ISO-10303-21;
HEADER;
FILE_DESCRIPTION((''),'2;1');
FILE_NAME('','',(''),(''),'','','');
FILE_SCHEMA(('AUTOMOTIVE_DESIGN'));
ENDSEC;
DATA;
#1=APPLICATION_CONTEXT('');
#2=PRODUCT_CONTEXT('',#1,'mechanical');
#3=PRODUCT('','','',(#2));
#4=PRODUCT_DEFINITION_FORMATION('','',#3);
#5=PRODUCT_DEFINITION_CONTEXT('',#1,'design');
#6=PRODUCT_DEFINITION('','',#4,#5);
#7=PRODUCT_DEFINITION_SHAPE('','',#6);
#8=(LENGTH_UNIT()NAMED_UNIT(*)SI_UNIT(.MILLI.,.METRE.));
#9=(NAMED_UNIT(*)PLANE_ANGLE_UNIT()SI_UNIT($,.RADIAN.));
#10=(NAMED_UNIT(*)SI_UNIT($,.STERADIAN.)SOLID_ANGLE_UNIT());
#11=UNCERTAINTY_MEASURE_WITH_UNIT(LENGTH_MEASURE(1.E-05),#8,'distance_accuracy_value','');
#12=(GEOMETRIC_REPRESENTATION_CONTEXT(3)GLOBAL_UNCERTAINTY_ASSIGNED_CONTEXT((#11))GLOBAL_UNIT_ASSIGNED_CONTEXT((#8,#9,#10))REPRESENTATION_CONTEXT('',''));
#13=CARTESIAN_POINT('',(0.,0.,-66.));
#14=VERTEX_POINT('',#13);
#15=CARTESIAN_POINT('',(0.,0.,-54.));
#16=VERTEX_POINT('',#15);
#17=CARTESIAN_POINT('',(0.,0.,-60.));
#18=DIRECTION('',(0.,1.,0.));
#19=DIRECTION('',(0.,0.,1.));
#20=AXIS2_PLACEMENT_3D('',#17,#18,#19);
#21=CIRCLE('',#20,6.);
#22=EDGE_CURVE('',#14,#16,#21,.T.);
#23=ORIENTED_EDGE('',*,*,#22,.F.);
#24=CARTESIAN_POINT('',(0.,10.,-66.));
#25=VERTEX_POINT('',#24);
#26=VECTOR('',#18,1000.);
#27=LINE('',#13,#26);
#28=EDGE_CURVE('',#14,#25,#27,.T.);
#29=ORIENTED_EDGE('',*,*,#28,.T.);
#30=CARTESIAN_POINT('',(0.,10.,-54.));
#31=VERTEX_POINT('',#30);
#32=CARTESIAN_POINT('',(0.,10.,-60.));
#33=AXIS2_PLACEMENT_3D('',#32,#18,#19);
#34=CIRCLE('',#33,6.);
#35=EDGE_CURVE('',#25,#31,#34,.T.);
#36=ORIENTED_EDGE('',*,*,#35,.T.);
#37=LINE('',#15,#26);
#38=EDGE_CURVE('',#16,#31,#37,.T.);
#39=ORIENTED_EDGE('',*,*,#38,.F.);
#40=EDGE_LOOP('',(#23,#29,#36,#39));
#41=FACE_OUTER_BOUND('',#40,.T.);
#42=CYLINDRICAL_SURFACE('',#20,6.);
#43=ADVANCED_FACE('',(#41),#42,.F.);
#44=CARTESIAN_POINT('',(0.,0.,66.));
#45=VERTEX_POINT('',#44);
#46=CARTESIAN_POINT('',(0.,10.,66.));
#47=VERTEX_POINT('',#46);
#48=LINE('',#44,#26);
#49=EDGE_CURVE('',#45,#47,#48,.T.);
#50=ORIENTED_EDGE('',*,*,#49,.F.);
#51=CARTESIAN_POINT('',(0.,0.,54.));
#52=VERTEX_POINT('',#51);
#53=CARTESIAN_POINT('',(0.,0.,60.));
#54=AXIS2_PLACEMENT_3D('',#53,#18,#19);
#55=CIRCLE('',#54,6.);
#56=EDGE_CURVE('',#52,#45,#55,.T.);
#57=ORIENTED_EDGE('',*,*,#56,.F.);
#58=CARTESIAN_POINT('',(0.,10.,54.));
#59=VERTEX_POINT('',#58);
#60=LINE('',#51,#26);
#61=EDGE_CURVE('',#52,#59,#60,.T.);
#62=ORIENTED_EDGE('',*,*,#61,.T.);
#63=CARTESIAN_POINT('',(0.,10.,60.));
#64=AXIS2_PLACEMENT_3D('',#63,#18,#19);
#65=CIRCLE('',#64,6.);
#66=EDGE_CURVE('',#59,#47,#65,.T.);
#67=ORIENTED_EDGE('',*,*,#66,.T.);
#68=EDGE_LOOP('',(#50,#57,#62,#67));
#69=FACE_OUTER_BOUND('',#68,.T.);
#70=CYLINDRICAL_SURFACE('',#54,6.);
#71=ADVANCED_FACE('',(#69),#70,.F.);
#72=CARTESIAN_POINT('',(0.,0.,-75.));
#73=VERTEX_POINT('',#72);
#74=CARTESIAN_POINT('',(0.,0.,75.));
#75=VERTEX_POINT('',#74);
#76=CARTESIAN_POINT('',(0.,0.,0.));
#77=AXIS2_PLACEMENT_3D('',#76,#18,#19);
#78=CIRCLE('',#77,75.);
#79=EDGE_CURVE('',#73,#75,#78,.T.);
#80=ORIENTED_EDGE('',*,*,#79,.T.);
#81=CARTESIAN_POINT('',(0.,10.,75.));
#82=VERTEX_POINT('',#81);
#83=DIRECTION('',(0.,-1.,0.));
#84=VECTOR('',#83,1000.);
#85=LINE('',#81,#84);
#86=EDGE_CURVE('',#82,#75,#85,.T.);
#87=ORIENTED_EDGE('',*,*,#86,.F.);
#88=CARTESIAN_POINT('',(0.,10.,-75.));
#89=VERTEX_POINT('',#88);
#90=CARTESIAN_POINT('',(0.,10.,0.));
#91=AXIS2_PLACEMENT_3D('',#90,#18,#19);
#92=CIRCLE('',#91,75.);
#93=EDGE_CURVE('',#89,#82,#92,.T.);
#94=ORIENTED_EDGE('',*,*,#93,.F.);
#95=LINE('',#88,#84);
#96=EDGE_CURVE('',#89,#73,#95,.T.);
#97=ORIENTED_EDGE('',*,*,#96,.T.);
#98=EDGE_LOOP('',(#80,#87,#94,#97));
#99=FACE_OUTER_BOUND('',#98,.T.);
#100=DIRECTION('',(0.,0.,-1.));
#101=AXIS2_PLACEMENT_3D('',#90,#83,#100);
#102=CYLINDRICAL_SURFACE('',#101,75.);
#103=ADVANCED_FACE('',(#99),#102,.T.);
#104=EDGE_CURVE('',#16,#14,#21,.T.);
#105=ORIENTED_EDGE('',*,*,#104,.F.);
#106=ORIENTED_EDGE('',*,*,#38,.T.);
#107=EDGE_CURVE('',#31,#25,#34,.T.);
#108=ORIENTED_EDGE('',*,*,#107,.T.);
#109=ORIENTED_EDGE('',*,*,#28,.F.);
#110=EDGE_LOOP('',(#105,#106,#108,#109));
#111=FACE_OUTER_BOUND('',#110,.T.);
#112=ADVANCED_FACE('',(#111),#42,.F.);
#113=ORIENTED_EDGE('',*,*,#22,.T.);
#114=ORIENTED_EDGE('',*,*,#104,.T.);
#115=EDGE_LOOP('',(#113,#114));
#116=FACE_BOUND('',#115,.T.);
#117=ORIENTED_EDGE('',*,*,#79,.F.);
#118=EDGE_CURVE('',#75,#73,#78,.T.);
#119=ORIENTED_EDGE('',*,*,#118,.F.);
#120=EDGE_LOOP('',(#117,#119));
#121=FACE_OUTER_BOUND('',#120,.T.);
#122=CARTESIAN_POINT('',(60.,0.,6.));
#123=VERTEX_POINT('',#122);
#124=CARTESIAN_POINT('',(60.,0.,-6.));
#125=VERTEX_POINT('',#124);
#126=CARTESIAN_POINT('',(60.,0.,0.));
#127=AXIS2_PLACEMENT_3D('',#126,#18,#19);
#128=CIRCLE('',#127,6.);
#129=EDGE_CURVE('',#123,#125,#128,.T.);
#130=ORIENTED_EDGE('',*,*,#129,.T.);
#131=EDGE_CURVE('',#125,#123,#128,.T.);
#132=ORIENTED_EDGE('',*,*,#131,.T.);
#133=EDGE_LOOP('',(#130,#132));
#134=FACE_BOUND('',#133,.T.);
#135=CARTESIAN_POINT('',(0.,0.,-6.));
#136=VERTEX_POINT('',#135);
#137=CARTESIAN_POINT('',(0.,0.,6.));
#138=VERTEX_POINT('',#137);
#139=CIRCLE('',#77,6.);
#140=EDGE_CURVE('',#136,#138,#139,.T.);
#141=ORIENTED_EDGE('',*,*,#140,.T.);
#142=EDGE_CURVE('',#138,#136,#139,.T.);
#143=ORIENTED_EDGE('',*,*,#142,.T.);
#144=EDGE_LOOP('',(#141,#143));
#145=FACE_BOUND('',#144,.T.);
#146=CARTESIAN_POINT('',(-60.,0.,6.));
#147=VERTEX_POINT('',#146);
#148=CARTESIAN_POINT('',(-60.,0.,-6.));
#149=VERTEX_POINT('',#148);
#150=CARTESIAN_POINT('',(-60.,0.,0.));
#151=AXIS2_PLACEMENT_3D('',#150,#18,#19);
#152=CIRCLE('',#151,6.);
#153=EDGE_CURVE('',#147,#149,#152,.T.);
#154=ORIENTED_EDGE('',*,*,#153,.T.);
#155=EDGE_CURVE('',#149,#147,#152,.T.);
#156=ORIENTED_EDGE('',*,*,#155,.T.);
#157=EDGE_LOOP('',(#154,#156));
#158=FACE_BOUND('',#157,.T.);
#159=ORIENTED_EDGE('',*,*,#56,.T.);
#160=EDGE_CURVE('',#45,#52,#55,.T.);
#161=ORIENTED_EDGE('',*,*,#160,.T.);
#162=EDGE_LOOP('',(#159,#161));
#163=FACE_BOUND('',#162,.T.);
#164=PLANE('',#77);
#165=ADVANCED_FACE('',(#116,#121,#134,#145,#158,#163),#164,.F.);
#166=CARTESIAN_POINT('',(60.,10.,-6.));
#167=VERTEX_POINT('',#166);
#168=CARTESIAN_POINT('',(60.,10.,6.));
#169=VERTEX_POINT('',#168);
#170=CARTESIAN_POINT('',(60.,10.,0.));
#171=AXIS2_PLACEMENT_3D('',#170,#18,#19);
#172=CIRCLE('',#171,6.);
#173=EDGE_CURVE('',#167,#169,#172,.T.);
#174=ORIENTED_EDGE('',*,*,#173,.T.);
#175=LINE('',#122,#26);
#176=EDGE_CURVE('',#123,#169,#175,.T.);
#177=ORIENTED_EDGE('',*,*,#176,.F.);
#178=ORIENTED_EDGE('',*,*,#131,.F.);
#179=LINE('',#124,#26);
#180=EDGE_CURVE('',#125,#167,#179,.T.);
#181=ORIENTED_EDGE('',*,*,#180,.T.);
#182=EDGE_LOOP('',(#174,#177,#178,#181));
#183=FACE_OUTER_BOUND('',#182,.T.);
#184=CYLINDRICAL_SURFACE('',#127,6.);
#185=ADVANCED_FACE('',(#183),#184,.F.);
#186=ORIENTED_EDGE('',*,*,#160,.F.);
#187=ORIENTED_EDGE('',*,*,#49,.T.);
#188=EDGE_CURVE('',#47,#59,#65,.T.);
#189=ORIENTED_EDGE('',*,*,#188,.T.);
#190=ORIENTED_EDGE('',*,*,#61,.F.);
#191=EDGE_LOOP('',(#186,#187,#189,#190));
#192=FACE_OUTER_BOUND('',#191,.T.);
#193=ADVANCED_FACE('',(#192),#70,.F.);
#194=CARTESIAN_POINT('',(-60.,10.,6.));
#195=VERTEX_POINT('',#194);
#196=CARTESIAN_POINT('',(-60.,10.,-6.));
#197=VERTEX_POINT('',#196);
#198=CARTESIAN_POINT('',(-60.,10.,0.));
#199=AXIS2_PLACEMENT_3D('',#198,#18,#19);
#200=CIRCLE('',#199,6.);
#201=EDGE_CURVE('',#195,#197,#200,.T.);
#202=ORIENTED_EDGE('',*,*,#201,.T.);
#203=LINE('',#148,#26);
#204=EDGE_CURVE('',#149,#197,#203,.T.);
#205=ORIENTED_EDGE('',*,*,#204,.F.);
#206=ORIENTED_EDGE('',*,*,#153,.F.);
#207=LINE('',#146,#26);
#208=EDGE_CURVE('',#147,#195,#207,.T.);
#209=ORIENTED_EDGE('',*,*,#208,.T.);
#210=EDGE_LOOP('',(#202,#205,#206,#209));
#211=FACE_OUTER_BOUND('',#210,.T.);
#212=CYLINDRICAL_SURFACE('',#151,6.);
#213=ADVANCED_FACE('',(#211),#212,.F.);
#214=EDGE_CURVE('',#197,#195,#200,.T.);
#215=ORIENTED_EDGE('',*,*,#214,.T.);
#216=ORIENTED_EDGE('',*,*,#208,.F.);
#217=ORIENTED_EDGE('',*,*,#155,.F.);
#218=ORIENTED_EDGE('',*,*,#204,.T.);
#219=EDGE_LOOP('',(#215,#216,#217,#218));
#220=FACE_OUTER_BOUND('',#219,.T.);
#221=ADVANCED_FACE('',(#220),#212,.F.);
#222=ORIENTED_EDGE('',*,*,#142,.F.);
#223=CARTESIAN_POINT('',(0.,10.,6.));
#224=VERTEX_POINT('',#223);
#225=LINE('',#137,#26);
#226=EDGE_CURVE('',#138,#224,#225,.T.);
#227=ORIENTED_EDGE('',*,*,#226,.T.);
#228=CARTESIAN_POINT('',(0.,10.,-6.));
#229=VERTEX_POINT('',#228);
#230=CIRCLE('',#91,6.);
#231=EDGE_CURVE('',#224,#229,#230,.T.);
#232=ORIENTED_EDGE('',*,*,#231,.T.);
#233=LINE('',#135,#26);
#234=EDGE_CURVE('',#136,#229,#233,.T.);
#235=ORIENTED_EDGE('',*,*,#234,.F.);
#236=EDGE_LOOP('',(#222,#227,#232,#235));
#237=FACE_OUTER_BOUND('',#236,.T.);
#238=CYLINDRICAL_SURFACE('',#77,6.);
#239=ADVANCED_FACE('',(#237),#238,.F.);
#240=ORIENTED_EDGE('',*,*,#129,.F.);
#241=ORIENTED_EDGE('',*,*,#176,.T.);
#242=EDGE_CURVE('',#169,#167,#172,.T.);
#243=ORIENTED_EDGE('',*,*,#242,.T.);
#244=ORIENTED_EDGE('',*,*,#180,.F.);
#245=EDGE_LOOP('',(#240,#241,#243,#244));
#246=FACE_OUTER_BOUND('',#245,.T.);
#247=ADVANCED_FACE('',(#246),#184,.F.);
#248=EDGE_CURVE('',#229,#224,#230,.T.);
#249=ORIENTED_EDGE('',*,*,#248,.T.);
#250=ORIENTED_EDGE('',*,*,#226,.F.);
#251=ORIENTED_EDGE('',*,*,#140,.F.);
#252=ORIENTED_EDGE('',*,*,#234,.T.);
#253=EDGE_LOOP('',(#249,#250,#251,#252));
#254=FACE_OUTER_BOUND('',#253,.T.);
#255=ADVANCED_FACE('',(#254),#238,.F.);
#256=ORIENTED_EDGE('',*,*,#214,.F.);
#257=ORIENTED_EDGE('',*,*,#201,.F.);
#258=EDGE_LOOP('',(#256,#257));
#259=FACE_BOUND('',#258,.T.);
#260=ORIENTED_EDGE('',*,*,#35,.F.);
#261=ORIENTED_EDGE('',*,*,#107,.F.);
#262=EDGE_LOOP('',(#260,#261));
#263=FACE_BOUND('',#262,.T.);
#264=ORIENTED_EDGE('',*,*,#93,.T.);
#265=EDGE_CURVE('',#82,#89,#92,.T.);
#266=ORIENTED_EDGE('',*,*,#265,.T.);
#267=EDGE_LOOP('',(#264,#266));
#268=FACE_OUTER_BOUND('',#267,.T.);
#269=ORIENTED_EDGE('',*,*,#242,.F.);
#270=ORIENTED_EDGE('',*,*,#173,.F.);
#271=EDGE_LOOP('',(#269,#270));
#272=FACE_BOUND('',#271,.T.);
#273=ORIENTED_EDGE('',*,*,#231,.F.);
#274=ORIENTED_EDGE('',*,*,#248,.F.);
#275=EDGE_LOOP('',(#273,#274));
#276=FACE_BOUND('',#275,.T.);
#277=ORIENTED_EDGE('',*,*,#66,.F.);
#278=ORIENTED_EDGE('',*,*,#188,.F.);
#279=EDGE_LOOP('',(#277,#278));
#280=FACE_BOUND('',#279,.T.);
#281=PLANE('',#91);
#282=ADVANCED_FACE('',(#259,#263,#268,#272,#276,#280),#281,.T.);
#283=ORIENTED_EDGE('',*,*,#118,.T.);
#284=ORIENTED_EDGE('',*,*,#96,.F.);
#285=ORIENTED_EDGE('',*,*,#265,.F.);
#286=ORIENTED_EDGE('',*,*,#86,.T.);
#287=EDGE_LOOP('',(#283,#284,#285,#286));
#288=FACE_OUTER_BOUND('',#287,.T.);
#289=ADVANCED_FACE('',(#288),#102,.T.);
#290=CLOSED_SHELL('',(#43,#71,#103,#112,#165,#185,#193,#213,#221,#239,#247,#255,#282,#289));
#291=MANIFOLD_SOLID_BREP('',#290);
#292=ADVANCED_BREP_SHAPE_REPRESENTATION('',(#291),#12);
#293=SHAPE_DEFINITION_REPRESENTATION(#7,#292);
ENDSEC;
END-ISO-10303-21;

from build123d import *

# Parameters (mm, degrees)
SKETCH1_R           = 75
BOSS_EXTRUDE1_DEPTH = 10
SKETCH2_R           = 6
CUT_EXTRUDE1_DEPTH  = 107.536378763


with BuildPart() as part:
    # Sketch1 → Boss-Extrude1 (new body)
    with BuildSketch(Plane(origin=(0, 0, 0), x_dir=(1, 0, 0), z_dir=(0, 1, 0))):
        with Locations(Location((0, 0, 0), (0, 0, 270))):
            Circle(SKETCH1_R)
    extrude(amount=BOSS_EXTRUDE1_DEPTH)

    # Sketch2 → Cut-Extrude1 (cut, through all)
    with BuildSketch(Plane(origin=(0, 10, 0), x_dir=(1, 0, 0), z_dir=(0, 1, 0))):
        with Locations(Location((0, 60, 0), (0, 0, 270))):
            Circle(SKETCH2_R)
        with Locations(Location((0, 0, 0), (0, 0, 270))):
            Circle(SKETCH2_R)
        with Locations(Location((0, -60, 0), (0, 0, 270))):
            Circle(SKETCH2_R)
        with Locations(Location((-60, 0, 0), (0, 0, 270))):
            Circle(SKETCH2_R)
        with Locations(Location((60, 0, 0), (0, 0, 270))):
            Circle(SKETCH2_R)
    extrude(amount=-CUT_EXTRUDE1_DEPTH, mode=Mode.SUBTRACT)


solid = part.part
